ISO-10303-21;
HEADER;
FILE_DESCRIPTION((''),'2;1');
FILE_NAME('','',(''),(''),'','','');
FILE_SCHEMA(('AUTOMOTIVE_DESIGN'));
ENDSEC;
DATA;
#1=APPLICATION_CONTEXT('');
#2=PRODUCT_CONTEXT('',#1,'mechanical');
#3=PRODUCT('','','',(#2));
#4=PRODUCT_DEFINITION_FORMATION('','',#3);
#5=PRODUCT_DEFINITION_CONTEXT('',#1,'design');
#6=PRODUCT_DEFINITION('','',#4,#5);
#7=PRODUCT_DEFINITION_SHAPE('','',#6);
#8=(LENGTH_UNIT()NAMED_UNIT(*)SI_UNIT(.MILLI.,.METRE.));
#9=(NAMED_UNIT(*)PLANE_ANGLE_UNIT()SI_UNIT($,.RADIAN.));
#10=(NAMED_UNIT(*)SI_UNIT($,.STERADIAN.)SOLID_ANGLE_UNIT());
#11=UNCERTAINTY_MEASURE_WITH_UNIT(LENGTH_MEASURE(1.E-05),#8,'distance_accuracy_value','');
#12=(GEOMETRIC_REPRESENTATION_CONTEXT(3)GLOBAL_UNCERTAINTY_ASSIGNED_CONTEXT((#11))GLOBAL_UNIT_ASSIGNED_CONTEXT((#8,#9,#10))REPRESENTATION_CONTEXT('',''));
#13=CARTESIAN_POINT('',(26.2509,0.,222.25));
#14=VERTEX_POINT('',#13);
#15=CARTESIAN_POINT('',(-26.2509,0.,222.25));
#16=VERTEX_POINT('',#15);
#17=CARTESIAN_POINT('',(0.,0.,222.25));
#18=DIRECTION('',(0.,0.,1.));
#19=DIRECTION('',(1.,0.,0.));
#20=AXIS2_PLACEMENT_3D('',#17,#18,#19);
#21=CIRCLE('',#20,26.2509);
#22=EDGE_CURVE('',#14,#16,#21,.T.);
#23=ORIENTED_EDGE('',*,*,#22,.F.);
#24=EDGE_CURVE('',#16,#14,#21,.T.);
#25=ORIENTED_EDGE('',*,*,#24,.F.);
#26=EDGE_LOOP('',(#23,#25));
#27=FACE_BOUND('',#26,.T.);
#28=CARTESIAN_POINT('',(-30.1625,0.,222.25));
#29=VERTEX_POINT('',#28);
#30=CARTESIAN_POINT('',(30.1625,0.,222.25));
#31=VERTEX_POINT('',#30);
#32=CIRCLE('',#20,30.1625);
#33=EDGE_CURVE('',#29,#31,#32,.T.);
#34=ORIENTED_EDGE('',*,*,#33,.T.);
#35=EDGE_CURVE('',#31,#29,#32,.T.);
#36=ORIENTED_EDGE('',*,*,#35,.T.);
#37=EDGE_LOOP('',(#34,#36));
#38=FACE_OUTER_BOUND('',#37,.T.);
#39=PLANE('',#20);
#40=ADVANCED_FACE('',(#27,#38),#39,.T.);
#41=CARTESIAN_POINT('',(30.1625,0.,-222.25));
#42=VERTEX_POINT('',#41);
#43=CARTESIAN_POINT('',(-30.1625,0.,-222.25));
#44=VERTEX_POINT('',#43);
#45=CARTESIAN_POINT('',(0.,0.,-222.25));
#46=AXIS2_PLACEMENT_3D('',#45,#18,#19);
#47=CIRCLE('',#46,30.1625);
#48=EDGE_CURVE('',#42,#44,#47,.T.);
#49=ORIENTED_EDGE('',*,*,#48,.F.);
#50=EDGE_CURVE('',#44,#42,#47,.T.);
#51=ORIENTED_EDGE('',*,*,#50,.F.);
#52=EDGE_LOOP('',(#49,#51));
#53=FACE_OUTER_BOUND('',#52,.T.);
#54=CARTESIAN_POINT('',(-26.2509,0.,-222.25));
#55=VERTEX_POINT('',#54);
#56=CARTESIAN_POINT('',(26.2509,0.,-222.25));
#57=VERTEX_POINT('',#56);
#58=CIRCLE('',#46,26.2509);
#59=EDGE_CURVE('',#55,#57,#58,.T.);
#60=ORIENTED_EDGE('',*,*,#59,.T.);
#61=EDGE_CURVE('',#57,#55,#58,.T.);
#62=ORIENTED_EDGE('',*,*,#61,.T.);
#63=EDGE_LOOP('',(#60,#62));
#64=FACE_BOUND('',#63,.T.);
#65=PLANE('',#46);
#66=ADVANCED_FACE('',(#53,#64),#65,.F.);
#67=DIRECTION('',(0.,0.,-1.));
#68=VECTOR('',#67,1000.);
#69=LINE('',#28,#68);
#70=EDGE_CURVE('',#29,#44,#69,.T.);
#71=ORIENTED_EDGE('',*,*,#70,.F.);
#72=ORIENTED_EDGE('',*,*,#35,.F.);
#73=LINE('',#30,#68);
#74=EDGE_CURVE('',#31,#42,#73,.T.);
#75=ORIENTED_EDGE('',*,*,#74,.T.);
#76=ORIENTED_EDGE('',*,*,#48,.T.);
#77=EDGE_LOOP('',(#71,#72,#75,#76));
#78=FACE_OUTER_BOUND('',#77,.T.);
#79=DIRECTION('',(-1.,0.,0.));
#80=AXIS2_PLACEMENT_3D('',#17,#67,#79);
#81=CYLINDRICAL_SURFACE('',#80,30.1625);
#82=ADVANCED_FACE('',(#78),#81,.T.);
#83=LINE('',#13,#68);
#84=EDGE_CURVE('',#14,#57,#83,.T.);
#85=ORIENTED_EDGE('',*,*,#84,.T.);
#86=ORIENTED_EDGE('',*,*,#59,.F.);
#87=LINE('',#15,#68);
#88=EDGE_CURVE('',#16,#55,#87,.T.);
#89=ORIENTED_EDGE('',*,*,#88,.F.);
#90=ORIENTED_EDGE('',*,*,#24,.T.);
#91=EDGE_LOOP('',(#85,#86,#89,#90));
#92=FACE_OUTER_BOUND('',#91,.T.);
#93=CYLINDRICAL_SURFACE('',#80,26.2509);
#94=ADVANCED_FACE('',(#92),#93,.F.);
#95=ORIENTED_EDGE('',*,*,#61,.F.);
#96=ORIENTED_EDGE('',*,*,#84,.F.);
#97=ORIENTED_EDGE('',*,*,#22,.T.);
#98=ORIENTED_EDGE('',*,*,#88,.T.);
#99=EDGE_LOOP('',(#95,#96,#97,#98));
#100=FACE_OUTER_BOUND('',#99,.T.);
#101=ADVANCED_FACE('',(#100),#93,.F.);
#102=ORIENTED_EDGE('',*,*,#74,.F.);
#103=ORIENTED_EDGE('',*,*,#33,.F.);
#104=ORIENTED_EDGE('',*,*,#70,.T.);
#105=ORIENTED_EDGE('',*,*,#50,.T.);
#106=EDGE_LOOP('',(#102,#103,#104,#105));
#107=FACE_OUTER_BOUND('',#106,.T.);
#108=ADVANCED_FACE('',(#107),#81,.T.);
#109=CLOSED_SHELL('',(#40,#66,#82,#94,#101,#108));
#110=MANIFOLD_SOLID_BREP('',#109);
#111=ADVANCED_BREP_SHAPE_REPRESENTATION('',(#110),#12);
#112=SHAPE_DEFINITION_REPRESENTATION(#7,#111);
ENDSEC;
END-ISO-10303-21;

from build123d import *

# Parameters (mm, degrees)
BOSS_EXTRUDE1_DEPTH      = 222.25
BOSS_EXTRUDE1_DEPTH_BACK = 222.25
SKETCH1_R                = 30.1625
SKETCH1_R_2              = 26.2509


with BuildPart() as part:
    # Sketch1 → Boss-Extrude1 (new, two sides: drawn at the far end of the back side and taken through both)
    with BuildSketch(Plane.XY.offset(-BOSS_EXTRUDE1_DEPTH_BACK)):
        Circle(SKETCH1_R)
        Circle(SKETCH1_R_2, mode=Mode.SUBTRACT)
    extrude(amount=BOSS_EXTRUDE1_DEPTH + BOSS_EXTRUDE1_DEPTH_BACK)


solid = part.part
